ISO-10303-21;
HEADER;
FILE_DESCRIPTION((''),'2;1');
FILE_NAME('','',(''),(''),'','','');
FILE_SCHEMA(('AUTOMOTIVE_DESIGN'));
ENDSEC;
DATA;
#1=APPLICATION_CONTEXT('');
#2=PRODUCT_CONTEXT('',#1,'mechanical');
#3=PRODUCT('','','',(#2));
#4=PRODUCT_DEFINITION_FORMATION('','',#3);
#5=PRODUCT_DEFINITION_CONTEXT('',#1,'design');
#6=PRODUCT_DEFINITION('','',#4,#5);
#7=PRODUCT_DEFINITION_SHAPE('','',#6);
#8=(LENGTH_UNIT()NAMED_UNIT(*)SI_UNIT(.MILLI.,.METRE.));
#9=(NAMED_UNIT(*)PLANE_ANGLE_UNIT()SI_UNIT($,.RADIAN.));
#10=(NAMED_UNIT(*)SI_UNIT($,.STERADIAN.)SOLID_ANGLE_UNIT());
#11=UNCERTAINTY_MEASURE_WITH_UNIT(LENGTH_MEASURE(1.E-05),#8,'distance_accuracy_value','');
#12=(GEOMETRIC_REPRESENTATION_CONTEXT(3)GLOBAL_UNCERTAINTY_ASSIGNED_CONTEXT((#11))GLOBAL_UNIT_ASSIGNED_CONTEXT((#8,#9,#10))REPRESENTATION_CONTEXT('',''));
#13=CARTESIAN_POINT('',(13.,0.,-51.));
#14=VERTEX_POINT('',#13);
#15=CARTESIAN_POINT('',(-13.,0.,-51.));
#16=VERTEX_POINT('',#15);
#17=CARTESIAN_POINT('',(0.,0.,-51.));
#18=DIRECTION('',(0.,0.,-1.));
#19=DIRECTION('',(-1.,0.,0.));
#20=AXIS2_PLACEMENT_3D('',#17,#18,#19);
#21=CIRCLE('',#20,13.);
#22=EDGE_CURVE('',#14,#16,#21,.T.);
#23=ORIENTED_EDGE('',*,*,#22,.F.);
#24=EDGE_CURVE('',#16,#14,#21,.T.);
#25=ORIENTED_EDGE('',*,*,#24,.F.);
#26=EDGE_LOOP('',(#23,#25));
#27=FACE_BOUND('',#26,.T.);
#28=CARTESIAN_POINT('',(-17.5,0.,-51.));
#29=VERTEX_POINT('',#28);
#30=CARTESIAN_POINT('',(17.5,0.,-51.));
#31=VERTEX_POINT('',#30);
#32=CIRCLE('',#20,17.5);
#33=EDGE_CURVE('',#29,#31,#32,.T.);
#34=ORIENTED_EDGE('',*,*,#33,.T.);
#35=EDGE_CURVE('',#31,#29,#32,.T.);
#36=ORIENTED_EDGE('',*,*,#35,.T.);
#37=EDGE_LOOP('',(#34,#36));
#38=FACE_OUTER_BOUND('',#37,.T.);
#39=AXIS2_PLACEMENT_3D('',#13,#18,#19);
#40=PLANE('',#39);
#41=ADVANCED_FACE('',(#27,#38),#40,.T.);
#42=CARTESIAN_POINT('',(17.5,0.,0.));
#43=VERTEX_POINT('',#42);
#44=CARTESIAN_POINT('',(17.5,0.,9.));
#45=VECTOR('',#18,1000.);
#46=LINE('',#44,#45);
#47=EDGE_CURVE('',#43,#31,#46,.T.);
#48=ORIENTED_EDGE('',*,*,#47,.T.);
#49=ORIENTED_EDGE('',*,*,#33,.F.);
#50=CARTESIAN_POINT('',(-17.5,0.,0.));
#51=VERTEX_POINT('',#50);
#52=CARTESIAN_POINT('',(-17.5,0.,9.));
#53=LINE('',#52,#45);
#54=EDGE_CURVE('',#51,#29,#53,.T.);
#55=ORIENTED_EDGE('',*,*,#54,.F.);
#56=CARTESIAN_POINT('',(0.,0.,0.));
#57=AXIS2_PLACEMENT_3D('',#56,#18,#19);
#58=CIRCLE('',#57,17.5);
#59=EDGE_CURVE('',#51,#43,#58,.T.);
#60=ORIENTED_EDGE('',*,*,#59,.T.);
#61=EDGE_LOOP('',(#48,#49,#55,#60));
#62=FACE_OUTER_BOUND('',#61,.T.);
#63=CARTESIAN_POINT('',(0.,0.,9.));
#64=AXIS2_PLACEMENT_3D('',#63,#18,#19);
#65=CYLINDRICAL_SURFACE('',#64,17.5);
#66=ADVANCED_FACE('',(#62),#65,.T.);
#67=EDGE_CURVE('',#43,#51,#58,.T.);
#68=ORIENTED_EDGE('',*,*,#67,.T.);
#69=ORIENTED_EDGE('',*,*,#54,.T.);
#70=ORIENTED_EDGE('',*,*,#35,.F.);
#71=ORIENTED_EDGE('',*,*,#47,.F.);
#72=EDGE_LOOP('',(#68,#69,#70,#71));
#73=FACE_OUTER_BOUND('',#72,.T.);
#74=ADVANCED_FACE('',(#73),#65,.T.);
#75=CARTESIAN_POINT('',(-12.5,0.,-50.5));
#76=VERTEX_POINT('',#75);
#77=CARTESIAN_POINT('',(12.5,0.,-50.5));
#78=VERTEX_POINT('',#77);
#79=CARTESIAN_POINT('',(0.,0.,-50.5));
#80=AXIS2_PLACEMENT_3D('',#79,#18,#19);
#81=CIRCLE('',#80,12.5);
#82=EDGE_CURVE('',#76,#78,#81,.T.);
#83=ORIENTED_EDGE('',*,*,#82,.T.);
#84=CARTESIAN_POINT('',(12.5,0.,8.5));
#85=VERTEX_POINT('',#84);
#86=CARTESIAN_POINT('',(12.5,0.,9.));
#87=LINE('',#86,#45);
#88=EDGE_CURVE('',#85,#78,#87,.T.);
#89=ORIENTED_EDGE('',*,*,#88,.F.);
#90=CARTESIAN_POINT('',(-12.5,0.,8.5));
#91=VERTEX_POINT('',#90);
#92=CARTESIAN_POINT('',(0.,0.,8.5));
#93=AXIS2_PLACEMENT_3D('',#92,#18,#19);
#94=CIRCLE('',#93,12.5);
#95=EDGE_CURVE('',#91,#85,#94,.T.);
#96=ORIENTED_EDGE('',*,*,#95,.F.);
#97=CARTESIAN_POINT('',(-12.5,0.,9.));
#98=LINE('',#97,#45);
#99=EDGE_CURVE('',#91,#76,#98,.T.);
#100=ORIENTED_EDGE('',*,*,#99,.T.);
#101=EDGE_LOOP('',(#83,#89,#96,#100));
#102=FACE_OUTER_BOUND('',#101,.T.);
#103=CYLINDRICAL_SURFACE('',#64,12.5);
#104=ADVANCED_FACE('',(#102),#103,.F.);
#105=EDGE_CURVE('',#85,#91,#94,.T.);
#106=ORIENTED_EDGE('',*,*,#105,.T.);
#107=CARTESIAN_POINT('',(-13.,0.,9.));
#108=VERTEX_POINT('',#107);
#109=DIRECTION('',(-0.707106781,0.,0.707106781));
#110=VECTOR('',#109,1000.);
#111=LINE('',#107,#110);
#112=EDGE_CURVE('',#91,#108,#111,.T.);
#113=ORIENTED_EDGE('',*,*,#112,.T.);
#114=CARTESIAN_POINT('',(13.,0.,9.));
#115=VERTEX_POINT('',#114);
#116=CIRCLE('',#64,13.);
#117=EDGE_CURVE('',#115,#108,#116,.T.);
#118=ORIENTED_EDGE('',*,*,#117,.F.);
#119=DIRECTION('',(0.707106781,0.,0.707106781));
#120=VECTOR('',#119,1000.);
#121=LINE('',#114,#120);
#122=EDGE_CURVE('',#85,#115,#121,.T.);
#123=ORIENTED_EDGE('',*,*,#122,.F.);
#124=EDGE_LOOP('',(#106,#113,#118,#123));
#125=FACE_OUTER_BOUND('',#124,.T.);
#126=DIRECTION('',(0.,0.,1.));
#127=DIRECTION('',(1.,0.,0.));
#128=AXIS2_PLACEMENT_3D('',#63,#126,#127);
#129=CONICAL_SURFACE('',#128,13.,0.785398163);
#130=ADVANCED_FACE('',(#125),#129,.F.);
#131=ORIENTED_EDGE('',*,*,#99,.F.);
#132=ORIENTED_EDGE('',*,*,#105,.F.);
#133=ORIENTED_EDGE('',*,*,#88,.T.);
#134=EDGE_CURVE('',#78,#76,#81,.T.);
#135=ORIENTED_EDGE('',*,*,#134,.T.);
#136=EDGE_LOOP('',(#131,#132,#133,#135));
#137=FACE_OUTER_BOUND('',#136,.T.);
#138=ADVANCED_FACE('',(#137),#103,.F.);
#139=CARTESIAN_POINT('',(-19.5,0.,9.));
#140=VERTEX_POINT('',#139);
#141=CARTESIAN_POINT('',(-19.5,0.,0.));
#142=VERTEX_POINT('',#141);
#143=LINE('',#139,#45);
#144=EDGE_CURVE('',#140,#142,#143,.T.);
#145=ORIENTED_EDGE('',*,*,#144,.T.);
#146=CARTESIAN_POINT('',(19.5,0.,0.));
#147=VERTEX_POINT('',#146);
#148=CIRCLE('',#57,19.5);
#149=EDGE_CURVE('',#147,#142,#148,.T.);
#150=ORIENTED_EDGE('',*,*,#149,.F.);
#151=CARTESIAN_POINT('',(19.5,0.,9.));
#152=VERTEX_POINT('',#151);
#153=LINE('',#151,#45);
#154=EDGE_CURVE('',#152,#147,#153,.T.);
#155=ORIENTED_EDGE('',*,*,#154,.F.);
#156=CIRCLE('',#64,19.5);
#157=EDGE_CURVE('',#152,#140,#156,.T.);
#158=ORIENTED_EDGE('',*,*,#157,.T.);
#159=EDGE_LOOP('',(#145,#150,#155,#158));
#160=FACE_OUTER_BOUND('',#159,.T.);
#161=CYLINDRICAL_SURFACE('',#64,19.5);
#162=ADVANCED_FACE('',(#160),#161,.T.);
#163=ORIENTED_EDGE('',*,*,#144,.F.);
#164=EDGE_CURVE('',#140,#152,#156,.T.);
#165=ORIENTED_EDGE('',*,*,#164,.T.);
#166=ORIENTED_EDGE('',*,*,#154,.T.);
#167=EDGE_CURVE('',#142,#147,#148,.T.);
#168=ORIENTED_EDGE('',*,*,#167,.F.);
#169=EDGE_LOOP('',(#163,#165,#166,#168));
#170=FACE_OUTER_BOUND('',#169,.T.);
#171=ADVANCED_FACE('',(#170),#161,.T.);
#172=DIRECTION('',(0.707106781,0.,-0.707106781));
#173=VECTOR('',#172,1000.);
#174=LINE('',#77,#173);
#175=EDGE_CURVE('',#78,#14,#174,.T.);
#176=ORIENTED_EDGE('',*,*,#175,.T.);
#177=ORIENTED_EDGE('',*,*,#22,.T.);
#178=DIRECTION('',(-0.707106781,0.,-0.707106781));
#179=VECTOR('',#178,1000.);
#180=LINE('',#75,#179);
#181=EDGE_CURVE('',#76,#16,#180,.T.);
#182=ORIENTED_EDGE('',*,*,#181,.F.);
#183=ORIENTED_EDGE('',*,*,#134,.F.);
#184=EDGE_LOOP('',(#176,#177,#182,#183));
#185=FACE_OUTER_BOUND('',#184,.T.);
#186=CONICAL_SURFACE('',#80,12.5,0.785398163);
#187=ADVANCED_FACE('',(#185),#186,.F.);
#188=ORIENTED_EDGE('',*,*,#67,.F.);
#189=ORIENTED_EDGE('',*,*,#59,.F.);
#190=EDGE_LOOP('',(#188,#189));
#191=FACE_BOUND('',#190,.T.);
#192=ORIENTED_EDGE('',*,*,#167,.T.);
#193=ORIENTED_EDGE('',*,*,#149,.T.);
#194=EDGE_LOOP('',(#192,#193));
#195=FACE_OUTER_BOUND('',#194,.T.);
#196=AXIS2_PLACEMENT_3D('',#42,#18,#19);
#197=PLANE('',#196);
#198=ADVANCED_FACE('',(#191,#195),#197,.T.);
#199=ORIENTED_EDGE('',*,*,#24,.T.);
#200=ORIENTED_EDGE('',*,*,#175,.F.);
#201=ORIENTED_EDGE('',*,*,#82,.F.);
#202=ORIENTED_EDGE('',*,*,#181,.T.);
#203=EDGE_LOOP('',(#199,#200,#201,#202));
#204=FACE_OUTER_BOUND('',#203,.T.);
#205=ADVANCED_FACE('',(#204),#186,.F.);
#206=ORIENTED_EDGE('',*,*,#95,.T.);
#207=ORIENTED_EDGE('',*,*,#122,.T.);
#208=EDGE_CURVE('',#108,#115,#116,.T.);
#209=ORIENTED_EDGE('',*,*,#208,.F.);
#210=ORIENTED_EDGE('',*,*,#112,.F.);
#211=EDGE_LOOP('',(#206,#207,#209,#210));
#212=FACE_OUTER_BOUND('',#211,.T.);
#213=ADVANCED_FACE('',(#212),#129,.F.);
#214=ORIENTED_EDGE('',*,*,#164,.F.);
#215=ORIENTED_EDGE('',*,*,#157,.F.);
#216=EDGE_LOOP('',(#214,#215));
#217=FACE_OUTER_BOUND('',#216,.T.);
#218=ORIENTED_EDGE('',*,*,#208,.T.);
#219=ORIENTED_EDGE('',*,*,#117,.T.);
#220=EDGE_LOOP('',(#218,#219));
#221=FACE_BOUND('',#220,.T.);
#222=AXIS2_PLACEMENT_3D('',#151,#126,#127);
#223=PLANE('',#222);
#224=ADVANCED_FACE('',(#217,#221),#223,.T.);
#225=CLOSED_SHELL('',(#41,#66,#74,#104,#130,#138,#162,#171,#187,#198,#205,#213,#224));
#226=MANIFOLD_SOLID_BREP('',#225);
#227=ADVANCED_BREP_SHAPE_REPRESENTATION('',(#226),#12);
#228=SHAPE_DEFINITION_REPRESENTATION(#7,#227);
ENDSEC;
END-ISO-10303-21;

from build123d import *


with BuildPart() as part:
    # Sketch1 → Revolve1 (revolve)
    with BuildSketch(Plane.XZ, mode=Mode.PRIVATE) as revolve1_sk:
        Polygon((19.5, 0), (19.5, 9), (13, 9), (12.5, 8.5), (12.5, -50.5), (13, -51), (17.5, -51), (17.5, 0), align=None)
    revolve(revolve1_sk.sketch.rotate(Axis((0, 0, 9), (0, 0, -1)), 180), axis=Axis((0, 0, 9), (0, 0, -1)))


solid = part.part
